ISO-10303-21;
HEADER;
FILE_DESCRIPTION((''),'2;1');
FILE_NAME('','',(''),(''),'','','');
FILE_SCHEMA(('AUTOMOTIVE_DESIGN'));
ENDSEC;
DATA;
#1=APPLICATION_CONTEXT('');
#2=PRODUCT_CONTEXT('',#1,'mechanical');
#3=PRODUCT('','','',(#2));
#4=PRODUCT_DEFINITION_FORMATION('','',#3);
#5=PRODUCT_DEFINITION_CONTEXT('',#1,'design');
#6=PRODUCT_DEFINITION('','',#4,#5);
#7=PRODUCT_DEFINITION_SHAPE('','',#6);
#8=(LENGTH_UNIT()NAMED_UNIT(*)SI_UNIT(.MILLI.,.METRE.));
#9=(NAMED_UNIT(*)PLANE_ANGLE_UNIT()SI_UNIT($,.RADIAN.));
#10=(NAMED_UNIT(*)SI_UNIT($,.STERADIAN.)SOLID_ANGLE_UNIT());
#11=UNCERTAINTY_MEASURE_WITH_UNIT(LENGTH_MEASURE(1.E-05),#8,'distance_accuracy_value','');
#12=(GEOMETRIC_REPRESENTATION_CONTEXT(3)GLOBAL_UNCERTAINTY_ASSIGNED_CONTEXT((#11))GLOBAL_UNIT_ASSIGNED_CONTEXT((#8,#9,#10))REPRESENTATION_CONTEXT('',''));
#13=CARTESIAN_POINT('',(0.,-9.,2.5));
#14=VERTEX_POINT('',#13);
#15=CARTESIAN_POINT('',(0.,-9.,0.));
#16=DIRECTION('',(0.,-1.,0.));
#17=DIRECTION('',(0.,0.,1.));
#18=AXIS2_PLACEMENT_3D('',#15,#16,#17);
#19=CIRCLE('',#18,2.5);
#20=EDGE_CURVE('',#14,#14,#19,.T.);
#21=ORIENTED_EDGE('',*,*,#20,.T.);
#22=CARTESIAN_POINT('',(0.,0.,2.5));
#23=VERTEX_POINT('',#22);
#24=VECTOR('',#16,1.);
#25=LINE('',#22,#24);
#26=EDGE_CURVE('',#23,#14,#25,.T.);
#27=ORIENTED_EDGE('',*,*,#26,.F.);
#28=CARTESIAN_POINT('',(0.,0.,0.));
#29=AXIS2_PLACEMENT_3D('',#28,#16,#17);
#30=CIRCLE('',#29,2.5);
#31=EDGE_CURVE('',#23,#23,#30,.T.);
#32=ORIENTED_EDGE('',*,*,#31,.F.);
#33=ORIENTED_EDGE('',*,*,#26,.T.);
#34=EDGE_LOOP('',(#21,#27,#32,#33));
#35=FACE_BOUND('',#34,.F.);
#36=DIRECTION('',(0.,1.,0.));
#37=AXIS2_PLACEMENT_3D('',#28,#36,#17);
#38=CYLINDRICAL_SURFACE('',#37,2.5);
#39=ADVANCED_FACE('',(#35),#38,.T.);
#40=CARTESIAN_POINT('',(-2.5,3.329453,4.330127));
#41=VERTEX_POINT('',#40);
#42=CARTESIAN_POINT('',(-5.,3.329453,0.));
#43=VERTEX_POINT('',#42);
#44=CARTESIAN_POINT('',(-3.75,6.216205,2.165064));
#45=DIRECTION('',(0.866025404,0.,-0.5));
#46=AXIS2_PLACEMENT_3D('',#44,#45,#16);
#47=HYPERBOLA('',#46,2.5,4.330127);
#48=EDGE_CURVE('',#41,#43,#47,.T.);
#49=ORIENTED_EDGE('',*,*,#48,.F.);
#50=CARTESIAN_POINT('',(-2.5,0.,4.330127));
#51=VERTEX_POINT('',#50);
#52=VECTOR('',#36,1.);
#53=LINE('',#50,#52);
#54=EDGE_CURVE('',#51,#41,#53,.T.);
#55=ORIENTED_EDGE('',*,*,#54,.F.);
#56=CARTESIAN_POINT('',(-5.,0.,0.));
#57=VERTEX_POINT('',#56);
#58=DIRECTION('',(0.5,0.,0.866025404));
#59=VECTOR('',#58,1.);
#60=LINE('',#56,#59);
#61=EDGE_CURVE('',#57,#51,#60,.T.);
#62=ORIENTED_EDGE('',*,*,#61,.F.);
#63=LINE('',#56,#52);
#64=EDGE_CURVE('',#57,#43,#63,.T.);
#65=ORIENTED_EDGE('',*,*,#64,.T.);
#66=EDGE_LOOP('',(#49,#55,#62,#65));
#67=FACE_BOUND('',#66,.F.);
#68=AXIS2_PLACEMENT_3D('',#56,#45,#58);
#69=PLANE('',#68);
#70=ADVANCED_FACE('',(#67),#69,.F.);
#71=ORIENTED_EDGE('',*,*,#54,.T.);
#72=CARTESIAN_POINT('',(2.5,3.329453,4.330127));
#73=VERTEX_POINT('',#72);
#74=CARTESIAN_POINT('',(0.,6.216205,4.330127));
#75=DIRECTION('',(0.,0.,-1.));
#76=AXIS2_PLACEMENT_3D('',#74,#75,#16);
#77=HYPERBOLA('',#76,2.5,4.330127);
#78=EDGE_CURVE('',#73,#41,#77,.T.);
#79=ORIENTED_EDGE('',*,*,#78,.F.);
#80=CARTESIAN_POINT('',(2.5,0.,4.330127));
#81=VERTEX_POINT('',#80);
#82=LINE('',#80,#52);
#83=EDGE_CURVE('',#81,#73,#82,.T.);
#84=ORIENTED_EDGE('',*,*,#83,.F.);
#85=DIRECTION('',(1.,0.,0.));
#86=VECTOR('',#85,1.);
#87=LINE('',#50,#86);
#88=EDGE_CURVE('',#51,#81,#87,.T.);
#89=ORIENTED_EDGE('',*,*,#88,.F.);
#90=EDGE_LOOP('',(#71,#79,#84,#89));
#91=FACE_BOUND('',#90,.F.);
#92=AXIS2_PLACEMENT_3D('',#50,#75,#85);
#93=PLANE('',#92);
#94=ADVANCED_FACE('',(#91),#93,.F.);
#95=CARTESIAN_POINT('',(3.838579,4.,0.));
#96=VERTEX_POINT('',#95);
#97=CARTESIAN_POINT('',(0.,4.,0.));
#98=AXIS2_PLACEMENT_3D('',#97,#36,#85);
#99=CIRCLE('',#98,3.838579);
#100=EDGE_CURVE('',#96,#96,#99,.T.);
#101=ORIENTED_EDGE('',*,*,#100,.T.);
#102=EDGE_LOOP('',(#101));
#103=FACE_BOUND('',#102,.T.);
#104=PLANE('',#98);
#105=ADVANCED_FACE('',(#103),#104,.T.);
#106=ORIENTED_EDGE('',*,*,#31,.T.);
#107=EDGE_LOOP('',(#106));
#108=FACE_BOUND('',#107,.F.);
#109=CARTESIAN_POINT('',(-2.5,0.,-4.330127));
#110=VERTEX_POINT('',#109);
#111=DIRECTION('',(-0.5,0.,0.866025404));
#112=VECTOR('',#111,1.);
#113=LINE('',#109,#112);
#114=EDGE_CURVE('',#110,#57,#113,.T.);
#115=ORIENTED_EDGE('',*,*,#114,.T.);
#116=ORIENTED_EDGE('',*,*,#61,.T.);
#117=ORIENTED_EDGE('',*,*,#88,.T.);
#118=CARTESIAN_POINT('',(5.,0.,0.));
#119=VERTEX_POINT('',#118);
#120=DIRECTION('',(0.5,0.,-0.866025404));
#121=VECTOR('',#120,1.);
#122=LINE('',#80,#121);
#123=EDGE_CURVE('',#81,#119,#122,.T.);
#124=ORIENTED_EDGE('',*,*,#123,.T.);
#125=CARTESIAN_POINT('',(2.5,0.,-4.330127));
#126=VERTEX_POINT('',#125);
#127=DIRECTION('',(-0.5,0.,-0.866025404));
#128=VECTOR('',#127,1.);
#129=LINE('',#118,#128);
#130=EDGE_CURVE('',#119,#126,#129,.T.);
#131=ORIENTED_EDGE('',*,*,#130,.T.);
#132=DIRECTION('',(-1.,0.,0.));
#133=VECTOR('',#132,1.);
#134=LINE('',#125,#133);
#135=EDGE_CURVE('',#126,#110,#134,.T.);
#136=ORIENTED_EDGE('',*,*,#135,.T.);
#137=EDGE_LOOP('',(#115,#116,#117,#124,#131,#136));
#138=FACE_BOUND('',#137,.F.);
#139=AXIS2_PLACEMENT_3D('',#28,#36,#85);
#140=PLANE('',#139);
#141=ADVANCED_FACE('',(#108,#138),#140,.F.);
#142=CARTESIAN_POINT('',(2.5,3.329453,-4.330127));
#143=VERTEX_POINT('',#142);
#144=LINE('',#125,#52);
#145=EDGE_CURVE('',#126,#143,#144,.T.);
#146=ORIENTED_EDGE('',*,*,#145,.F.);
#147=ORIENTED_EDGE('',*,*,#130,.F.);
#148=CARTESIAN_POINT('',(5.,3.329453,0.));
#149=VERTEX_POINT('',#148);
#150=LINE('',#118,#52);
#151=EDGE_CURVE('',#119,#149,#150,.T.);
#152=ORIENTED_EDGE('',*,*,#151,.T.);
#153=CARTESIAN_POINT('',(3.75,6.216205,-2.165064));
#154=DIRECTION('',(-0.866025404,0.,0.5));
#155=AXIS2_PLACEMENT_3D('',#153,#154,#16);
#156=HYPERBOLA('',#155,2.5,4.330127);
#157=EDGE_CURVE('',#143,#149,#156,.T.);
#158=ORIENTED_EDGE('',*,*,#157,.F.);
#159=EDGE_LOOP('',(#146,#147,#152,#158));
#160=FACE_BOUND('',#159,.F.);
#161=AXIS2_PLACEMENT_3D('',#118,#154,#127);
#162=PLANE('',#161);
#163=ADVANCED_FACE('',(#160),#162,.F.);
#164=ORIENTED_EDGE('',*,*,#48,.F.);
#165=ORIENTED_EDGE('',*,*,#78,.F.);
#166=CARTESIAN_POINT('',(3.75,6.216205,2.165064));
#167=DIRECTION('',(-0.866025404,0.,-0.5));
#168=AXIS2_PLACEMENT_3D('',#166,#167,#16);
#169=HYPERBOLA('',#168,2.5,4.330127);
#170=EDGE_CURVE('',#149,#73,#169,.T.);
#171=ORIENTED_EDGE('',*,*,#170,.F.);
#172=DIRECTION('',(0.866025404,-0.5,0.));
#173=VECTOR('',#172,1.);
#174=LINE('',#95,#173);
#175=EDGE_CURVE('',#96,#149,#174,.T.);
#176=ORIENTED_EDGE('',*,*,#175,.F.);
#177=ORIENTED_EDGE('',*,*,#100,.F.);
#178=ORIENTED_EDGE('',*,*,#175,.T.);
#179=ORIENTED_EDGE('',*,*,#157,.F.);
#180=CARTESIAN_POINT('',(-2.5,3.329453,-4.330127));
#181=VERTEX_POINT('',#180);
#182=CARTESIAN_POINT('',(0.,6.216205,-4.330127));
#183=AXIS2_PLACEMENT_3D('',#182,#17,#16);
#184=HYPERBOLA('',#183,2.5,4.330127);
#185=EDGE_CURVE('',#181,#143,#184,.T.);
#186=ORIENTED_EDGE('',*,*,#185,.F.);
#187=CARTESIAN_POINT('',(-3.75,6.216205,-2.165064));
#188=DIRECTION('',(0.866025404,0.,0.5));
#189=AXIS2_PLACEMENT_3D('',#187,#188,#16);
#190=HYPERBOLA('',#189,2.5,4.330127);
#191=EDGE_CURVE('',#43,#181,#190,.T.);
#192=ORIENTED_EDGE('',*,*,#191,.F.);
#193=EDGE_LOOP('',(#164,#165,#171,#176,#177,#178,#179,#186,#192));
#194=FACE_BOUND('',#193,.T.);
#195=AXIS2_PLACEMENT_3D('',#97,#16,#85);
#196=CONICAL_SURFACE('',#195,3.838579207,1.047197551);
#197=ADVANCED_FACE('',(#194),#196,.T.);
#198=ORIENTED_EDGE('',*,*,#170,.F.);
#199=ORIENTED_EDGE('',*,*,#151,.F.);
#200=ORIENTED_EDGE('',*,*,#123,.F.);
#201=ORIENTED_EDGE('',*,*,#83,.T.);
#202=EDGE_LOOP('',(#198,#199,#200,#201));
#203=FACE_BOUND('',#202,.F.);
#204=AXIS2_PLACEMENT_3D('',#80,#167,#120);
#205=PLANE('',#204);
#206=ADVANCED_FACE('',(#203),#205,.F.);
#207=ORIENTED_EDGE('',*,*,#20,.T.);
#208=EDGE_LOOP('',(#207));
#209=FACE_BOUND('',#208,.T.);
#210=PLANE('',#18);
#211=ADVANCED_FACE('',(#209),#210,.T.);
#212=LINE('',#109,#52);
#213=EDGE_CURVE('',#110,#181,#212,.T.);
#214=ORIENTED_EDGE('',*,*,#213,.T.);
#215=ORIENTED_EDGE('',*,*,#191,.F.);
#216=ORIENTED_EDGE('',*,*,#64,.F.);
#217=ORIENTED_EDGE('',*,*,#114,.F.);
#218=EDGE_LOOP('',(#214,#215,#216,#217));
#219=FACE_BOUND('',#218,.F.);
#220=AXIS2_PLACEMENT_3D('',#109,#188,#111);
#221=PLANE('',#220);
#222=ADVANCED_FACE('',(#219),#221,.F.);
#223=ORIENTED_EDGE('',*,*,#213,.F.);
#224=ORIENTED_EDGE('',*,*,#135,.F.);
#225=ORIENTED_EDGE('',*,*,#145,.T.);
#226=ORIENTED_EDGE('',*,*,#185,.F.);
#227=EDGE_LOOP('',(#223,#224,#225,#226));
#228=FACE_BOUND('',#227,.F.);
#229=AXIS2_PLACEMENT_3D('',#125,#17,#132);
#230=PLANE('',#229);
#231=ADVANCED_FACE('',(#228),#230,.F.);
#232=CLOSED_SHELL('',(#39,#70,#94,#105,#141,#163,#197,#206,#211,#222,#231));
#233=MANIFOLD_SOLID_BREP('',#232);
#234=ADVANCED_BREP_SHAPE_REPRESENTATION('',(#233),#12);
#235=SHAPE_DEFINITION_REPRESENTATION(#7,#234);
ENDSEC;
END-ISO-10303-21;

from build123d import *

# Parameters (mm, degrees)
BOSS_EXTRUDE1_DEPTH = 4
SKETCH2_OUTSIDE_W   = 45.006
SKETCH2_OUTSIDE_H   = 43.666
SKETCH2_OUTSIDE_R   = 3.838579207
CUT_EXTRUDE1_DEPTH  = 8.729812417
CUT_EXTRUDE1_DRAFT  = -60
SKETCH3_R           = 2.5
BOSS_EXTRUDE2_DEPTH = 9


with BuildPart() as part:
    # Sketch1 → Boss-Extrude1 (new body)
    with BuildSketch(Plane(origin=(0, 0, 0), x_dir=(1, 0, 0), z_dir=(0, 1, 0))):
        Polygon((5, 0), (2.5, 4.330127019), (-2.5, 4.330127019), (-5, 0), (-2.5, -4.330127019), (2.5, -4.330127019), align=None)
    extrude(amount=BOSS_EXTRUDE1_DEPTH)


with BuildPart() as cut_extrude1_tool:
    # Sketch2 outside → Cut-Extrude1 (with draft: the straight prism first)
    with BuildSketch(Plane(origin=(0, 4, 0), x_dir=(1, 0, 0), z_dir=(0, 1, 0))):
        Rectangle(SKETCH2_OUTSIDE_W, SKETCH2_OUTSIDE_H)
        Circle(SKETCH2_OUTSIDE_R, mode=Mode.SUBTRACT)
    extrude(amount=-CUT_EXTRUDE1_DEPTH)
    # Cut-Extrude1: the draft: its side faces are tilted about the plane it starts from
    cut_extrude1_sides = [cut_extrude1_tool.faces().sort_by_distance(p)[0] for p in [
        (0, -0.364906208, 21.833),
        (22.503, -0.364906208, 0),
        (0, -0.364906208, -21.833),
        (-22.503, -0.364906208, 0),
        (-3.838579207, -0.364906208, 0),
    ]]
    draft(cut_extrude1_sides, Plane(origin=(0, 4, 0), x_dir=(1, 0, 0), z_dir=(0, 1, 0)), CUT_EXTRUDE1_DRAFT)


with BuildPart() as part_1:
    add(part.part)

    # Cut-Extrude1: cut by cut_extrude1_tool
    add(cut_extrude1_tool.part, mode=Mode.SUBTRACT)

    # Sketch3 → Boss-Extrude2 (add)
    with BuildSketch(Plane.XZ):
        with Locations(Location((0, 0, 0), (0, 0, 90))):
            Circle(SKETCH3_R)
    extrude(amount=BOSS_EXTRUDE2_DEPTH)


solid = part_1.part
